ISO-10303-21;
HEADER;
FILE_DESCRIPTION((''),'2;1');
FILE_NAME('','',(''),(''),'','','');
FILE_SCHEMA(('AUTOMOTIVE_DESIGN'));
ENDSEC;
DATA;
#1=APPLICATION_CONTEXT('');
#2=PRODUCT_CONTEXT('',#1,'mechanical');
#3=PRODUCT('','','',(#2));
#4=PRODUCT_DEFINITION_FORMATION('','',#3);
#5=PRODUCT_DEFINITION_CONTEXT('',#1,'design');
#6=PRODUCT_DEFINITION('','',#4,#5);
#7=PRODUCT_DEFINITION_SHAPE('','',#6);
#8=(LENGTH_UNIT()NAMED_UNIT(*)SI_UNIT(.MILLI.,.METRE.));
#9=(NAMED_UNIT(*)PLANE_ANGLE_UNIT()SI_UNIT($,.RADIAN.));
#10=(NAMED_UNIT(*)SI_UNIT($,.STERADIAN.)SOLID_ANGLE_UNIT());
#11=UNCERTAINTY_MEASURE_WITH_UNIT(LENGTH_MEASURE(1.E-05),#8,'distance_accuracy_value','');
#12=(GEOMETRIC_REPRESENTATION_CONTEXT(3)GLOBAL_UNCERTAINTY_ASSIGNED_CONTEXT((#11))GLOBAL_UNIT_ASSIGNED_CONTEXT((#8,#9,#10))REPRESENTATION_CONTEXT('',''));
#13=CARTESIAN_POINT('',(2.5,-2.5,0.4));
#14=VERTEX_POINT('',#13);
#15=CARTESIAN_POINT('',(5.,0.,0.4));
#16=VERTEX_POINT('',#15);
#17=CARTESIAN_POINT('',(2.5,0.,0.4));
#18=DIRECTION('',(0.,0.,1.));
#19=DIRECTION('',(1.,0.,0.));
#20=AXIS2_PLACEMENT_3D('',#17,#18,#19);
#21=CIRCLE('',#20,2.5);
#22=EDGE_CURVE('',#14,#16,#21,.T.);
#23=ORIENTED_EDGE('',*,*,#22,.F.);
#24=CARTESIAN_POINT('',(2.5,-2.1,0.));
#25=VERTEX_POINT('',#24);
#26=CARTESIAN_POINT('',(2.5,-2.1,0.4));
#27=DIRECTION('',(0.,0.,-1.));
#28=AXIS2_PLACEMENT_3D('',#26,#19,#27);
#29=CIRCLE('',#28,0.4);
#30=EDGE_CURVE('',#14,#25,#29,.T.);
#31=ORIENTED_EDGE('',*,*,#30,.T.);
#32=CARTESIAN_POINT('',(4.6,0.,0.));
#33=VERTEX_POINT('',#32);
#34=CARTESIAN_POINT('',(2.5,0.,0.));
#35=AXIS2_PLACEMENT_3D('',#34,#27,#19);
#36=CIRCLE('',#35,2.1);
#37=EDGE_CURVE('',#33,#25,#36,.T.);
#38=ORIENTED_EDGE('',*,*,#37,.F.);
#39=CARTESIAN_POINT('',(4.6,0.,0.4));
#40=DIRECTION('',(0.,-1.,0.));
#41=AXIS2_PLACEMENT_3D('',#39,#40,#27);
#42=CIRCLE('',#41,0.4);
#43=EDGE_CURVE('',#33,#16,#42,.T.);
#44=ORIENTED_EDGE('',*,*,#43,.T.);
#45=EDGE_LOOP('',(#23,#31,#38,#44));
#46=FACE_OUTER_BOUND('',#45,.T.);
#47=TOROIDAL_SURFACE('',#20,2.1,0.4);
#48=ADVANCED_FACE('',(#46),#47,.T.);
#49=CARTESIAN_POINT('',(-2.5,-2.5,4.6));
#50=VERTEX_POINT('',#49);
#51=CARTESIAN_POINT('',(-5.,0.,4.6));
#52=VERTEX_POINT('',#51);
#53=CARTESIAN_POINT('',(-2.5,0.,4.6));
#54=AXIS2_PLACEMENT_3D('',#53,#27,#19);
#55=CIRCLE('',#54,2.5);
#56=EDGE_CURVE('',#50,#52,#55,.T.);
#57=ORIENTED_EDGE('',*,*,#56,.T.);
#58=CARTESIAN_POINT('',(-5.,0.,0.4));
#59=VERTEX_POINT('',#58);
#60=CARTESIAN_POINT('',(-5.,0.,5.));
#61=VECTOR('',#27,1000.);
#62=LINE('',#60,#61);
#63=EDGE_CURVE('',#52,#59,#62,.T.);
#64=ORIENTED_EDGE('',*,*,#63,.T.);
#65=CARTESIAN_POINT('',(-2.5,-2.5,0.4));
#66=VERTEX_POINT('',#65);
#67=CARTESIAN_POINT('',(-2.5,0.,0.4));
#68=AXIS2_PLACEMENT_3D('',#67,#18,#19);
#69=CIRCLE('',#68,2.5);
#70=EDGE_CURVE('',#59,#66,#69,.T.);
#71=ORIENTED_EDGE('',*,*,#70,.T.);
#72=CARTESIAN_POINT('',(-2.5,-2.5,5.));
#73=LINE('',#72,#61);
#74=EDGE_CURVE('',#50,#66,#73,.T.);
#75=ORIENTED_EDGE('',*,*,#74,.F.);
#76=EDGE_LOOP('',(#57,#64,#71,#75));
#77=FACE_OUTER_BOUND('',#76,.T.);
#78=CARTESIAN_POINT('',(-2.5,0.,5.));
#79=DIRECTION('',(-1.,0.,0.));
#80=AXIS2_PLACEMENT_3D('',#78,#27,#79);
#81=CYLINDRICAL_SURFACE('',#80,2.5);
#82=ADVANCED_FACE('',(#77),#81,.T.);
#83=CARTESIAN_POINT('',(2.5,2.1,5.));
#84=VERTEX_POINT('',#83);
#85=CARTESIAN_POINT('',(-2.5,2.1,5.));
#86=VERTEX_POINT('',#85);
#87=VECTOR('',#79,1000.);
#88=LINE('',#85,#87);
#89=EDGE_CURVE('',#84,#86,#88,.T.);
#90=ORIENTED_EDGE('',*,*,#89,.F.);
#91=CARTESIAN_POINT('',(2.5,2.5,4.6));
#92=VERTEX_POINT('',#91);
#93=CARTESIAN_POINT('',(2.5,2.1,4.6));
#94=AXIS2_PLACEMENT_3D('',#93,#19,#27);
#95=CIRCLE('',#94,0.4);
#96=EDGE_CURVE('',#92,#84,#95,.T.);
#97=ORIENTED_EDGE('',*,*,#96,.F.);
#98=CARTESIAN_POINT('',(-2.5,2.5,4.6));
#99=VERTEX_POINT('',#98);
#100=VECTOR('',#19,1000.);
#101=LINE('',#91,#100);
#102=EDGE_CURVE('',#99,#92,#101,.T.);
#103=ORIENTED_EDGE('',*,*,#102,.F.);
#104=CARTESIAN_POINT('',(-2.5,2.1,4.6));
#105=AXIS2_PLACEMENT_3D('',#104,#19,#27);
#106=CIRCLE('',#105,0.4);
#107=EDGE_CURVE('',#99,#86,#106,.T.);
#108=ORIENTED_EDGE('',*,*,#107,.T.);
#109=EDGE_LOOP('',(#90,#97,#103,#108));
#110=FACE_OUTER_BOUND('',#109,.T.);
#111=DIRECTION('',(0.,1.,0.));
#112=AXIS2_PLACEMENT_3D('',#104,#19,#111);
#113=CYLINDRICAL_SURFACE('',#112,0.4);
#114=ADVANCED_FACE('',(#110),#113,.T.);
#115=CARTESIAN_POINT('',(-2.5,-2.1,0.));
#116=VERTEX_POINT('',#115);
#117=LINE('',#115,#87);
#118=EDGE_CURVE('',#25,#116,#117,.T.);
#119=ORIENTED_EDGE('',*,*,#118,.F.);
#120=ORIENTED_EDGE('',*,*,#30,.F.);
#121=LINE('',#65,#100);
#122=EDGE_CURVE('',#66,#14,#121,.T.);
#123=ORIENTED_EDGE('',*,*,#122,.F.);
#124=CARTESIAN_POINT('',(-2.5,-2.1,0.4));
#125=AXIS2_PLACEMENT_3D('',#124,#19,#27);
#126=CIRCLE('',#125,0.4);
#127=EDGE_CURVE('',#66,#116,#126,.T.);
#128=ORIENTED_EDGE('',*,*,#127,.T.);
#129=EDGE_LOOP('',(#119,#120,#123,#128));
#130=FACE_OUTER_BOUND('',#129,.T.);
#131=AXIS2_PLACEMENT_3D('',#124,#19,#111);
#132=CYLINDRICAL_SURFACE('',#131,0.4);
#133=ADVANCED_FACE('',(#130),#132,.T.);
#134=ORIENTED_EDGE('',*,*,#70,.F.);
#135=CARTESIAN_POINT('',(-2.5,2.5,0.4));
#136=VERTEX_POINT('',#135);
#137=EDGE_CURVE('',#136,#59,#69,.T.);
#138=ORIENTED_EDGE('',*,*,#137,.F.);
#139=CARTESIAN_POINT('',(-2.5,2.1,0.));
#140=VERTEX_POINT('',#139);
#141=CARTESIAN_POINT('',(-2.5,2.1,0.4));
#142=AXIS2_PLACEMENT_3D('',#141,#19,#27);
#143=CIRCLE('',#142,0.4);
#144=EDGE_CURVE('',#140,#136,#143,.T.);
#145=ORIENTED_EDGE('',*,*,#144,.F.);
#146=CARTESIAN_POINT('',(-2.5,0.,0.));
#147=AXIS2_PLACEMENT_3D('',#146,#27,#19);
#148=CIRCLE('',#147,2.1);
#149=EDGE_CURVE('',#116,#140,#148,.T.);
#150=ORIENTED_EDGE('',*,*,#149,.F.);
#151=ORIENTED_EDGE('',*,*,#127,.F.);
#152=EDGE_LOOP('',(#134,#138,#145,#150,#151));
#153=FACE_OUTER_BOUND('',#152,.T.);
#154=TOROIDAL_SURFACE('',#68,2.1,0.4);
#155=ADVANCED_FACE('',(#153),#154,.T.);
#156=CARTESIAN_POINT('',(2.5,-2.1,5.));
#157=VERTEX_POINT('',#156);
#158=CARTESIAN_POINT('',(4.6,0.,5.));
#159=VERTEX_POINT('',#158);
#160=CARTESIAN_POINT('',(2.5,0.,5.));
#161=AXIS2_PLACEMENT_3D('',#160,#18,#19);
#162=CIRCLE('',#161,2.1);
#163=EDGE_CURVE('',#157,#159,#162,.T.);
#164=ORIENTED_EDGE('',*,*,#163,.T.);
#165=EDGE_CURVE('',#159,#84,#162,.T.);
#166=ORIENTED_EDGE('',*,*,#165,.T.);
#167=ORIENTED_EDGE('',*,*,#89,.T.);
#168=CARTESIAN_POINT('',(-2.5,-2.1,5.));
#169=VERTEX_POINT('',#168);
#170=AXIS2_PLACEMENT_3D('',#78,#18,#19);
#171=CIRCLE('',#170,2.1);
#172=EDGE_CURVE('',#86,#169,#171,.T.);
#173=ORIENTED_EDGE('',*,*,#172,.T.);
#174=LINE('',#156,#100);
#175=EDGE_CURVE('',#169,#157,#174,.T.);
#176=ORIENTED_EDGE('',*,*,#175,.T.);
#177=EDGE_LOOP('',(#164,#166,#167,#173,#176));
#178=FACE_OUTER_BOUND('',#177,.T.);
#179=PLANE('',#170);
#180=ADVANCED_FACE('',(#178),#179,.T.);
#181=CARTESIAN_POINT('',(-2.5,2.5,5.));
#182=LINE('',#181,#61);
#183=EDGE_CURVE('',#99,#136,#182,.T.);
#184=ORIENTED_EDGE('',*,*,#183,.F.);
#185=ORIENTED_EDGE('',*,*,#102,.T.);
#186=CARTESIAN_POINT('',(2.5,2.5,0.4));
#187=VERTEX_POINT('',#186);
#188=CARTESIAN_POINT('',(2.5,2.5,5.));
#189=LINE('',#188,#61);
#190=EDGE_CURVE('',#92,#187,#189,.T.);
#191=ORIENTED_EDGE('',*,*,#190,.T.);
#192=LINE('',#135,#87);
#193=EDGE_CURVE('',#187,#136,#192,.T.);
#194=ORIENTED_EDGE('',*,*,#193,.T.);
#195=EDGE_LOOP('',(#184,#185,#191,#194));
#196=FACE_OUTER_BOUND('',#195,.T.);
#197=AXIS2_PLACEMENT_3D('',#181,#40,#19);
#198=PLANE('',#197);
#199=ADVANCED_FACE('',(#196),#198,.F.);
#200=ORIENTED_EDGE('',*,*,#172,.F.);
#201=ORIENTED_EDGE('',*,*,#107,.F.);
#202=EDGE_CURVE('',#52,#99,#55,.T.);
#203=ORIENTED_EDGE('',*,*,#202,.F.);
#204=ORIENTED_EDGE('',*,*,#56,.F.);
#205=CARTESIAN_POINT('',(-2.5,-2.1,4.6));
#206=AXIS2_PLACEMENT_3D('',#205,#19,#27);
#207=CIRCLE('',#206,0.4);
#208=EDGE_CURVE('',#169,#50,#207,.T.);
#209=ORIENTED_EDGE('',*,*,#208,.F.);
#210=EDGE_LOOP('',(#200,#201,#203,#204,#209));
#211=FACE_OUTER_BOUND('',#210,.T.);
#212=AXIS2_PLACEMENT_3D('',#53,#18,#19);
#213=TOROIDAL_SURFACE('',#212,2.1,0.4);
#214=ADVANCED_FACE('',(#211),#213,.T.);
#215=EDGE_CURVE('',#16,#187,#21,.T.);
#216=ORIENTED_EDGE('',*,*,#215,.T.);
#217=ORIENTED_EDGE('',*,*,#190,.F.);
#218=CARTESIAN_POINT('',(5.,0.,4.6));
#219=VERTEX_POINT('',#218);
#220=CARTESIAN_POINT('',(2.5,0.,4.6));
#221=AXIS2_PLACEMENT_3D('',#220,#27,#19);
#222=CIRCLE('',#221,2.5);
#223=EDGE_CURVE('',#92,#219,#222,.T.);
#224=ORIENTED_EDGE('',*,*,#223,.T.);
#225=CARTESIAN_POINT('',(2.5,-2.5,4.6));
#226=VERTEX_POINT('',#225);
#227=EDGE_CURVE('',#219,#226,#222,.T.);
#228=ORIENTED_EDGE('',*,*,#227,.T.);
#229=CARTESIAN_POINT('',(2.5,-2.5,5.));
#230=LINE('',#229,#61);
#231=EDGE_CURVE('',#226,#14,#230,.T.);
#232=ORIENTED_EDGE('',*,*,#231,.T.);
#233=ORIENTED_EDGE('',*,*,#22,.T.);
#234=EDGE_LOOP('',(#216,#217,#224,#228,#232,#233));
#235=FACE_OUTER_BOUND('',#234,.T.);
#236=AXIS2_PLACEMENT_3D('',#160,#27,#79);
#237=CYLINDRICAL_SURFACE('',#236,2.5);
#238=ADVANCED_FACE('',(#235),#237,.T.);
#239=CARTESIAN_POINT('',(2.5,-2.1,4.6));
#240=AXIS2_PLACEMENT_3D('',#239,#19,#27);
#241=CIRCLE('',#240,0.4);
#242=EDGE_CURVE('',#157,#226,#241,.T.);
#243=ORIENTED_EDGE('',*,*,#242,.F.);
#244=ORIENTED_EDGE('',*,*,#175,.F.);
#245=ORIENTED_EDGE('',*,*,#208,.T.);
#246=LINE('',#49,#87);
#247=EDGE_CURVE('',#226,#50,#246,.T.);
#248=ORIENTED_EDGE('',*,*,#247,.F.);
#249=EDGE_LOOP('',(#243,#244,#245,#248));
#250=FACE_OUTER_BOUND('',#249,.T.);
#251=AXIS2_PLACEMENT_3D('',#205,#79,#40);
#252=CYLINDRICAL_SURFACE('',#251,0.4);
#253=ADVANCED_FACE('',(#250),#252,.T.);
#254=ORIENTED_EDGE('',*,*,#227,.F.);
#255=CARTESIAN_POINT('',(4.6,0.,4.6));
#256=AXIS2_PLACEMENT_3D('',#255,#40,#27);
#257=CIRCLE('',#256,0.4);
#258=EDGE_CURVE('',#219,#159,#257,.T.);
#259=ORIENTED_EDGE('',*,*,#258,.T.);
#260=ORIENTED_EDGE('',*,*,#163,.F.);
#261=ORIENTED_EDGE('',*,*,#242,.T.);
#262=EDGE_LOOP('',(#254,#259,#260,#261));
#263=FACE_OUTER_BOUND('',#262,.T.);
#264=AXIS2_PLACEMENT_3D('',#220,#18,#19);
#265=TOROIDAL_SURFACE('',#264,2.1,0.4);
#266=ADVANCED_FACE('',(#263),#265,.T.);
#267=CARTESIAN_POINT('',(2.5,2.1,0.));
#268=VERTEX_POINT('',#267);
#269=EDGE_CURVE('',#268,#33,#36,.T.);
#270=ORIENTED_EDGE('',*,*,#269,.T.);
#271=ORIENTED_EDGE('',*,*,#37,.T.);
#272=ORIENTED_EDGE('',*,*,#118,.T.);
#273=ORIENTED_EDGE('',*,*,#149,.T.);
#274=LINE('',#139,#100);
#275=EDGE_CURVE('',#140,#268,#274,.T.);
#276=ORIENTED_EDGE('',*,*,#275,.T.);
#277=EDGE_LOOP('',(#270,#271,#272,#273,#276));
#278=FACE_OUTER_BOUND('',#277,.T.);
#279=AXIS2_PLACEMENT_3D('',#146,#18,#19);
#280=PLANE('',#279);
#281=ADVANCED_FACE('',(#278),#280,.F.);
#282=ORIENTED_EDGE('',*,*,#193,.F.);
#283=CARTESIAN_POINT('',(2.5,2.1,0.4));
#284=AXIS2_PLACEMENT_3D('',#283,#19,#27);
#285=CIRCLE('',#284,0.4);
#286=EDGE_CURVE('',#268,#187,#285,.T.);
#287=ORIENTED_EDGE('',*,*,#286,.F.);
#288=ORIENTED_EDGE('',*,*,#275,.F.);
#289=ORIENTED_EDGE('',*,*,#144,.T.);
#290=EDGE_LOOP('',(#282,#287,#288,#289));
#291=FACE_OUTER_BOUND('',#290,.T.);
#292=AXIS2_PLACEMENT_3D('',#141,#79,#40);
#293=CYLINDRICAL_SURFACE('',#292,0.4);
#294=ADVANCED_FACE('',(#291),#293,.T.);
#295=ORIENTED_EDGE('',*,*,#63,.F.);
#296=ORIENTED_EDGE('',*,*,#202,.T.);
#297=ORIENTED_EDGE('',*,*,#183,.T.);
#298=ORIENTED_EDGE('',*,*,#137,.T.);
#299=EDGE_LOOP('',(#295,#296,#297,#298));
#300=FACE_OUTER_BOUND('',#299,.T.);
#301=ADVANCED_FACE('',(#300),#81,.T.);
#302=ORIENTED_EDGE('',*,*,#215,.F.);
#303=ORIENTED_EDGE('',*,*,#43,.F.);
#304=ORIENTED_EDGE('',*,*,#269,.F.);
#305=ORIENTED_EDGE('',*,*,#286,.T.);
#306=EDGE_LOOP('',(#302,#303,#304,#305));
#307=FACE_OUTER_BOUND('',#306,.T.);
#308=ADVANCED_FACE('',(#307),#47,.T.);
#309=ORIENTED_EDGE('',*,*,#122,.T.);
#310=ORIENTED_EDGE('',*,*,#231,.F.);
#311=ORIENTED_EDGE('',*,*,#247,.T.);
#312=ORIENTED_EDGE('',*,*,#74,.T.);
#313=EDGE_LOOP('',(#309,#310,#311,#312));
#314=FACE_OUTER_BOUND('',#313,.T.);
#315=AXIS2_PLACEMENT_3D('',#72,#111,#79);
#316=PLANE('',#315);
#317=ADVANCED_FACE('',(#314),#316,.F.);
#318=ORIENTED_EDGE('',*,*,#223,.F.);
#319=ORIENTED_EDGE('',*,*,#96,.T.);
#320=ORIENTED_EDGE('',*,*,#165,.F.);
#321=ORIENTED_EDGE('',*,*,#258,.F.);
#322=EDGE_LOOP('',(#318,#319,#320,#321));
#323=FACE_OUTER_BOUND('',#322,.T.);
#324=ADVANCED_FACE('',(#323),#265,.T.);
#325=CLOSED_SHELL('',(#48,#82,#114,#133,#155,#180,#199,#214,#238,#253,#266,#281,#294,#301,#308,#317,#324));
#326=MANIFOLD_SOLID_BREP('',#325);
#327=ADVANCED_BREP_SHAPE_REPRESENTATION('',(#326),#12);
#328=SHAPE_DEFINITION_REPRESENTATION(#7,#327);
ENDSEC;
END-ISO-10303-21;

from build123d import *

# Parameters (mm, degrees)
EXTRUDE_527_DEPTH = 5
FILLET_1_R        = 0.4


with BuildPart() as part:
    # 草图1 → Extrude 527 (new body)
    with BuildSketch(Plane.XY):
        with BuildLine():
            Line((-2.5, 2.5), (2.5, 2.5))
            ThreePointArc((2.5, 2.5), (5, 0), (2.5, -2.5))
            Line((2.5, -2.5), (-2.5, -2.5))
            ThreePointArc((-2.5, -2.5), (-5, 0), (-2.5, 2.5))
        make_face()
    extrude(amount=EXTRUDE_527_DEPTH)

    # 圆角1
    fillet_1_edges = [part.edges().sort_by_distance(p)[0] for p in [
        (5, 0, 5),
        (0, 2.5, 5),
        (-5, 0, 5),
        (0, 2.5, 0),
        (5, 0, 0),
        (0, -2.5, 0),
        (-5, 0, 0),
        (0, -2.5, 5),
    ]]
    fillet(fillet_1_edges, radius=FILLET_1_R)


solid = part.part
